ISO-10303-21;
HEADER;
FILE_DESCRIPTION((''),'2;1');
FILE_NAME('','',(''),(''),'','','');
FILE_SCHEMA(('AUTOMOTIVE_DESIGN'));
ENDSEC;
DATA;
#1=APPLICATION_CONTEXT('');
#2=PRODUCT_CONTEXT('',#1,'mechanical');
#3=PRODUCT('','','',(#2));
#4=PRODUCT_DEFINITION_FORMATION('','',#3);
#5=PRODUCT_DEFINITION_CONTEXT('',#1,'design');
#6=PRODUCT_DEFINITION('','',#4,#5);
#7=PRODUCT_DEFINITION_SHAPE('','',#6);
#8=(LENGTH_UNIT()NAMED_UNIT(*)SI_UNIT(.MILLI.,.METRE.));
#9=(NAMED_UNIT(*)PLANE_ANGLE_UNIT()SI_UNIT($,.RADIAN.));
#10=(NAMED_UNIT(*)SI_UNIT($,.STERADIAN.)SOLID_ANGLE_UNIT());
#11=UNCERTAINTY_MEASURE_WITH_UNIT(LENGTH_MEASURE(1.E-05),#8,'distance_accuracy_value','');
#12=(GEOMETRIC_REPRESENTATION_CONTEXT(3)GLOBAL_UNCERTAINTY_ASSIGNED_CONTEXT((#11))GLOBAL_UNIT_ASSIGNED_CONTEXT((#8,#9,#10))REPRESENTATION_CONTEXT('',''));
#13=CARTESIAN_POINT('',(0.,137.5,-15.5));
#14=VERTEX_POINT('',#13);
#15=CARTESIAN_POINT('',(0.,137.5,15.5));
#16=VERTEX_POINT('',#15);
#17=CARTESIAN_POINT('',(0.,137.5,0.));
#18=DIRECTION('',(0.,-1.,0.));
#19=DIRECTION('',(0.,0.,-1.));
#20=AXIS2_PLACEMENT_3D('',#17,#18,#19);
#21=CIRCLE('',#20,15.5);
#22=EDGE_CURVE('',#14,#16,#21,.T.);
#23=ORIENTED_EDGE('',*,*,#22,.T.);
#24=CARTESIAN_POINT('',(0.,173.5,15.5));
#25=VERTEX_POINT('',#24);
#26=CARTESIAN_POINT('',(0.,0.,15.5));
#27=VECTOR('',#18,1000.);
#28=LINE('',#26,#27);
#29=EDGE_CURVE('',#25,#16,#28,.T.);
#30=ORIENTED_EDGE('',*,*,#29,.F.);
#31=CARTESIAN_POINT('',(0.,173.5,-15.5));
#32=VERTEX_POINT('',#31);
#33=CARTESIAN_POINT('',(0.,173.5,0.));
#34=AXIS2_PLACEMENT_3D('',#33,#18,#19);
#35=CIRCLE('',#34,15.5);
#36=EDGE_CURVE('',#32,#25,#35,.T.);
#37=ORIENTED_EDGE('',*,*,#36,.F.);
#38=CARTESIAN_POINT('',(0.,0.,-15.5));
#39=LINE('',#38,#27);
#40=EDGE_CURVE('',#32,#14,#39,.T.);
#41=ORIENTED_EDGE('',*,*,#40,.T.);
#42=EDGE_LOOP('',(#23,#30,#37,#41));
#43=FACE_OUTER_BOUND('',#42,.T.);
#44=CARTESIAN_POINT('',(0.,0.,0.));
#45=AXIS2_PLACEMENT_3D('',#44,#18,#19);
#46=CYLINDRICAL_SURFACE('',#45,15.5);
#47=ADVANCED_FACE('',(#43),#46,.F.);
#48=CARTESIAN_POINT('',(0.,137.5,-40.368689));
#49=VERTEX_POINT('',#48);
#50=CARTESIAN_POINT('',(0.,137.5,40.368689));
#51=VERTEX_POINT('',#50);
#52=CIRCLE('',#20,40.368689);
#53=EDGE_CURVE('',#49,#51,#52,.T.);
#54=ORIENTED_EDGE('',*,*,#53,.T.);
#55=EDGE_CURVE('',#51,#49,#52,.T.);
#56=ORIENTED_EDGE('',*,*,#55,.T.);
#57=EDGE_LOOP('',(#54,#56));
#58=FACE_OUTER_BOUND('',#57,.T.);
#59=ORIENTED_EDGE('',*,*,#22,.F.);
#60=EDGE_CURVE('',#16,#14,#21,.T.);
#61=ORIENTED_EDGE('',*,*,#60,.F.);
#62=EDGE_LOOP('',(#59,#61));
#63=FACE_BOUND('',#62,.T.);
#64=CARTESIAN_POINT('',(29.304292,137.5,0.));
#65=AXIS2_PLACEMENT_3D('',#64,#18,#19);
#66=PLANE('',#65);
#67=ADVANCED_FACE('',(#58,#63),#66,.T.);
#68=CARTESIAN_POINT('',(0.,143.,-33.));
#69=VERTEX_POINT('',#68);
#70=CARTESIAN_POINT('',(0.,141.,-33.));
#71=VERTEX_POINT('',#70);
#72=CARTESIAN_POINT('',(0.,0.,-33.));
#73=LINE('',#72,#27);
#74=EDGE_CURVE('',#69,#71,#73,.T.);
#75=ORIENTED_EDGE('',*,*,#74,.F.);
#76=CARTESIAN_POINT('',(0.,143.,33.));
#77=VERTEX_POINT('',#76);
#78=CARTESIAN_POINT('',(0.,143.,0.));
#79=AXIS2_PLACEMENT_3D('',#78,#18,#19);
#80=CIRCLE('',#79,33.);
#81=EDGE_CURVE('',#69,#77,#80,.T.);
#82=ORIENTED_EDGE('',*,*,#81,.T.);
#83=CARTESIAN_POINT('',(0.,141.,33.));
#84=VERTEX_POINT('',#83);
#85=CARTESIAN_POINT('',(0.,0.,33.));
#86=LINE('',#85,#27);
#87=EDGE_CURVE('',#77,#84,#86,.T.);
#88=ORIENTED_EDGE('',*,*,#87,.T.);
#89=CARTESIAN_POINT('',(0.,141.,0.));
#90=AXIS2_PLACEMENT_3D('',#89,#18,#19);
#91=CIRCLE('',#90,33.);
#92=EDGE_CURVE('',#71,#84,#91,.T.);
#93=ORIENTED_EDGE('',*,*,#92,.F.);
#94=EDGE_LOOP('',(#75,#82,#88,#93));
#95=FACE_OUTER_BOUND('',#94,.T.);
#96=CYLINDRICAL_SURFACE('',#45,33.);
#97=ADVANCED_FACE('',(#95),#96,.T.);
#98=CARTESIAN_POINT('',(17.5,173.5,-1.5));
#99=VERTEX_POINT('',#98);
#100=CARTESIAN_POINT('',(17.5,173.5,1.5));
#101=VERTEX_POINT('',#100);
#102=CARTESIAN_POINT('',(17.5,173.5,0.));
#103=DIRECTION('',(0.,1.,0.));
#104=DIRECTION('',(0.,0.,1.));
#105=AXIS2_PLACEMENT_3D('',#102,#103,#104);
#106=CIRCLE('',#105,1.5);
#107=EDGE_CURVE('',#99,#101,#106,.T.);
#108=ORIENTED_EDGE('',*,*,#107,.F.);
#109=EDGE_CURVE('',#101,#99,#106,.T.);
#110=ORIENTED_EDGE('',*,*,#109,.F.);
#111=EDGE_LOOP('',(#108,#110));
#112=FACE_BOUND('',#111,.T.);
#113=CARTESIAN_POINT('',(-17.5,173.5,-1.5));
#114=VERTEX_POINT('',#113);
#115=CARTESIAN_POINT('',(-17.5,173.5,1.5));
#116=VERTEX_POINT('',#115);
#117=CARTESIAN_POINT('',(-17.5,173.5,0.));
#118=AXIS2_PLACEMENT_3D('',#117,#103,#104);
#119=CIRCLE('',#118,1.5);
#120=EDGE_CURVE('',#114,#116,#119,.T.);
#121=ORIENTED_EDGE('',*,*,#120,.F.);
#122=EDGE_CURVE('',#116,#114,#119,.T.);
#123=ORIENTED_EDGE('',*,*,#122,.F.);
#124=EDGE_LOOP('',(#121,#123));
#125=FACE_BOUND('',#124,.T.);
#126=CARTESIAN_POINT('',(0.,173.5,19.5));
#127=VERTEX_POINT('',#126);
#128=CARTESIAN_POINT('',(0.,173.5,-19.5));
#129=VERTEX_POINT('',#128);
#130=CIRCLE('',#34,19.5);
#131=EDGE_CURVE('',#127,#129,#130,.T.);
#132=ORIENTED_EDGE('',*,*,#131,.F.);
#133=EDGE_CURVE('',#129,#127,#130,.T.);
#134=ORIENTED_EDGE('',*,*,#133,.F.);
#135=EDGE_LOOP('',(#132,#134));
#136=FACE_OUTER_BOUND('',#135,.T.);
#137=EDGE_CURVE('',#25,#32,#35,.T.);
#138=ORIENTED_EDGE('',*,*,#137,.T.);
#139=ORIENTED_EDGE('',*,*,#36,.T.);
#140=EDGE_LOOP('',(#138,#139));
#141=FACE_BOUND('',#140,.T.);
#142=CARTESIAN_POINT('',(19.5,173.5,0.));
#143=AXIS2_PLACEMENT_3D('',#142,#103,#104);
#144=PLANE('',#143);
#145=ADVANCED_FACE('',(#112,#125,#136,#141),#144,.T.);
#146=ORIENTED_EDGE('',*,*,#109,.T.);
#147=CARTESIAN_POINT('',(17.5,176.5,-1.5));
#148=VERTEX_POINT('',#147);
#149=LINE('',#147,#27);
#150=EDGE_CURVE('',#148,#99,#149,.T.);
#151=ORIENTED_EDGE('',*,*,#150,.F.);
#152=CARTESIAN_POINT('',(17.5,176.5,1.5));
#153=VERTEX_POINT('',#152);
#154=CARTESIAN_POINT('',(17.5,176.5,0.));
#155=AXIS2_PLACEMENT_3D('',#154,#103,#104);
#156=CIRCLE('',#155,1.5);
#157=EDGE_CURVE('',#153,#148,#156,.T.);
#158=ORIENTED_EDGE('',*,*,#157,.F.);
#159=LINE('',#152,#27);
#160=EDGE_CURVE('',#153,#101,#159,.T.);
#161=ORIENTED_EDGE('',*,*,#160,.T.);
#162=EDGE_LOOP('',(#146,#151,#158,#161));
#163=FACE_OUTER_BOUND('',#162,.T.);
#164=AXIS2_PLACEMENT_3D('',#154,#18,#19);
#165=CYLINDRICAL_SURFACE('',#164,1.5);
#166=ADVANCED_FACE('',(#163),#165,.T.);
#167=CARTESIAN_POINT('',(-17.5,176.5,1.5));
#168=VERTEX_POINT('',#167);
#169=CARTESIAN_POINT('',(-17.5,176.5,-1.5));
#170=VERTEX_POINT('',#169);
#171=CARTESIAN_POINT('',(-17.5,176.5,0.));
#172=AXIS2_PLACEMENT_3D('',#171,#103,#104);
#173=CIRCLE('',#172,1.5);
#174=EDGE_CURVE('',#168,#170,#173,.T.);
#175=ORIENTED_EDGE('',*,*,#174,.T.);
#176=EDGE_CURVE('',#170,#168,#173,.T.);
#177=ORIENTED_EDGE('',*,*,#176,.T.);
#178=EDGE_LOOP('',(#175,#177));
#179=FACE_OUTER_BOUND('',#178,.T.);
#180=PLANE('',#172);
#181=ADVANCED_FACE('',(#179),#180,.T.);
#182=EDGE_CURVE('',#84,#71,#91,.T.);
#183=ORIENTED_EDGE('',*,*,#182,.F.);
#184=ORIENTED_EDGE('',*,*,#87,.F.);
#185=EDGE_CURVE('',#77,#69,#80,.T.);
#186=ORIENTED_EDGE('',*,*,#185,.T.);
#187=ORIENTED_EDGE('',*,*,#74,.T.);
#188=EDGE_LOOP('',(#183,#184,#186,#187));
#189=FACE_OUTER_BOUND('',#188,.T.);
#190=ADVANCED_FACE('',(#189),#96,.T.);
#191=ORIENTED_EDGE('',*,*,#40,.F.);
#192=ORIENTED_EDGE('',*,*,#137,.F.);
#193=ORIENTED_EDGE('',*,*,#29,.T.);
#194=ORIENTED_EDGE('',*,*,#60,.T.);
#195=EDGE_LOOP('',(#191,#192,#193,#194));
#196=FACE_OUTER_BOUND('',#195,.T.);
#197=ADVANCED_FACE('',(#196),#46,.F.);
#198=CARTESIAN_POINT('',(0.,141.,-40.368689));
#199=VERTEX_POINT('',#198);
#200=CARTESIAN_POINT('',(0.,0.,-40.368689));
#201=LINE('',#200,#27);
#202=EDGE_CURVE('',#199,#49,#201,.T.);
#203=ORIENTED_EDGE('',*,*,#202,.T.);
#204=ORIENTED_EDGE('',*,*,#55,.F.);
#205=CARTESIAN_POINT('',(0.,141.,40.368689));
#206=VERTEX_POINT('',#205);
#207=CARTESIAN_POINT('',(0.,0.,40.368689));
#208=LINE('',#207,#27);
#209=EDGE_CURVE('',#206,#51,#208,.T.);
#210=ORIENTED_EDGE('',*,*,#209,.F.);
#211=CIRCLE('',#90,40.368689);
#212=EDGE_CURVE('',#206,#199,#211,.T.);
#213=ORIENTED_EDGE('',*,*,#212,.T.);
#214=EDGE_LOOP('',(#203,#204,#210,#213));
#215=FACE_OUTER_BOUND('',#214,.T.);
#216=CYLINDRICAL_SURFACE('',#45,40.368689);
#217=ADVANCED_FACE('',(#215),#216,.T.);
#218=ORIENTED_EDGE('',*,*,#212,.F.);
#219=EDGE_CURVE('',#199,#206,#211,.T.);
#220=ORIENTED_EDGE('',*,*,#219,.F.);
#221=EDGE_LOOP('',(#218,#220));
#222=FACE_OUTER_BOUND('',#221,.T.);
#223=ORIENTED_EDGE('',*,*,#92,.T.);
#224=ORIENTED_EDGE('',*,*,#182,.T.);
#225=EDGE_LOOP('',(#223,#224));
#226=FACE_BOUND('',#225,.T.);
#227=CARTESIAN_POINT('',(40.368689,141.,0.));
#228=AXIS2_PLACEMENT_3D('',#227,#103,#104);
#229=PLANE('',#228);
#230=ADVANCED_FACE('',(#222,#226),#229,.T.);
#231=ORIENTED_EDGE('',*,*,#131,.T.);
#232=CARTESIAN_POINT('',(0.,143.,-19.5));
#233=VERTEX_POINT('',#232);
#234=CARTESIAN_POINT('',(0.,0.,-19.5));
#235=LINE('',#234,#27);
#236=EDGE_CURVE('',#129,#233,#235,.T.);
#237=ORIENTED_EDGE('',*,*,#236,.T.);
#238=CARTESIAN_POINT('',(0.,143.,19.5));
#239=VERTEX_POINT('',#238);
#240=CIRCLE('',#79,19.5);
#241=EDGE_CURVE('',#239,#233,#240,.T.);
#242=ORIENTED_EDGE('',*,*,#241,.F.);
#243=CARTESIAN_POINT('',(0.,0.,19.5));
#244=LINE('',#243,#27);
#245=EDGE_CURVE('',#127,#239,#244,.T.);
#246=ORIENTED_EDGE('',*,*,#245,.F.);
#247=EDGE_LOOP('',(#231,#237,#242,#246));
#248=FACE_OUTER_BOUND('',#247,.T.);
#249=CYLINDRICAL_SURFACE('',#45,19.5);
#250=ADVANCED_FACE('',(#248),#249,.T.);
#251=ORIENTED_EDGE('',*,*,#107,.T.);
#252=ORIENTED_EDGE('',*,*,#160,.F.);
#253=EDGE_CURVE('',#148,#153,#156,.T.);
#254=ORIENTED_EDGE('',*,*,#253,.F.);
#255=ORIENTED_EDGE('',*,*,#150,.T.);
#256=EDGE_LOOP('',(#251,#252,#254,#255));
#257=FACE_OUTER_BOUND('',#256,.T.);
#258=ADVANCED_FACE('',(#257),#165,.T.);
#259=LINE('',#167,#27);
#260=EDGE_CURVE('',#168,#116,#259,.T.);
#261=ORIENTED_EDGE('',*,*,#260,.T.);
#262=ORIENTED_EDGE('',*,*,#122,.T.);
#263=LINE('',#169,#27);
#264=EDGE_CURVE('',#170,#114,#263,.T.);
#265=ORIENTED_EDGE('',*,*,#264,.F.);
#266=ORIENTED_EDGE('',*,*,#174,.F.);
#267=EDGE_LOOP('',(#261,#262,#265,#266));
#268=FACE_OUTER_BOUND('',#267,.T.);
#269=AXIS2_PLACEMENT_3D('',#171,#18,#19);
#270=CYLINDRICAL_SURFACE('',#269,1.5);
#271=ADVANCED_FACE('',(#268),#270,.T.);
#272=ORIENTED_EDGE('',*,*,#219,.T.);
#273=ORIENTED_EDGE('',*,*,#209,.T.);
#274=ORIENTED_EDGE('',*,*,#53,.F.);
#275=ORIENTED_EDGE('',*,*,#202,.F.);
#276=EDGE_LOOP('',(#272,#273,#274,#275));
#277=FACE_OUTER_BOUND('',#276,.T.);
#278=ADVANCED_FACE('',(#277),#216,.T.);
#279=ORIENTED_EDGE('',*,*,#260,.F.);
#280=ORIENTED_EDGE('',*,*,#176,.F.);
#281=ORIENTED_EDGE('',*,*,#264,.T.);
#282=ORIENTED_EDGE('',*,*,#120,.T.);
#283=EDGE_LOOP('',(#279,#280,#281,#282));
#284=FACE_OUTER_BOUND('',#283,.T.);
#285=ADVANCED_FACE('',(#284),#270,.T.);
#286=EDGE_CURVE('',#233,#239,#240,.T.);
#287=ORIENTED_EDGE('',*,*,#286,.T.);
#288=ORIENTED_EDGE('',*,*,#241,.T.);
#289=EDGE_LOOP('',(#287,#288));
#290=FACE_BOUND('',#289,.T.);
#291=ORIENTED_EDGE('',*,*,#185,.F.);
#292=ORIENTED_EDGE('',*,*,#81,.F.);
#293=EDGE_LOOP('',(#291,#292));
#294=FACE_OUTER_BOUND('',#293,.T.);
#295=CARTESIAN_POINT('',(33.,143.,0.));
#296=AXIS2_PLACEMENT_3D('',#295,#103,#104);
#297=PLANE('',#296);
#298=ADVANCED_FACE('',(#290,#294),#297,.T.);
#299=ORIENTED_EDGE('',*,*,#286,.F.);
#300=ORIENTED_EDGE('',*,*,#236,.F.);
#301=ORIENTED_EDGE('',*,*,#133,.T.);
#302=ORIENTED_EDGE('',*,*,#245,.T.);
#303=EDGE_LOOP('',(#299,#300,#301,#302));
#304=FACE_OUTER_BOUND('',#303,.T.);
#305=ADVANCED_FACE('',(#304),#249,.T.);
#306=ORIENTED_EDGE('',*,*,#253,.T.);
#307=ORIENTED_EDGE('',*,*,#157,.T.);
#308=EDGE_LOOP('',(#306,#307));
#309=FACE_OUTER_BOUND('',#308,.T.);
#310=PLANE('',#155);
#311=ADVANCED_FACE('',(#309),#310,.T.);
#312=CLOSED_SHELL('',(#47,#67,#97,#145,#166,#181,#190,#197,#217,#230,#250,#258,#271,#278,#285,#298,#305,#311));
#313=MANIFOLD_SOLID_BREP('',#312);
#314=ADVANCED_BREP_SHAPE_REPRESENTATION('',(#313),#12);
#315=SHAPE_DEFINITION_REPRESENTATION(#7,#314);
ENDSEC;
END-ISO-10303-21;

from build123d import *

# Parameters (mm, degrees)
SKETCH2_R           = 1.5
BOSS_EXTRUDE1_DEPTH = 3


with BuildPart() as part:
    # Sketch1 → Revolve1 (revolve)
    with BuildSketch(Plane.XY, mode=Mode.PRIVATE) as revolve1_sk:
        Polygon((40.368689296, 141), (33, 141), (33, 143), (19.5, 143), (19.5, 173.5), (15.5, 173.5), (15.5, 137.5), (29.304292175, 137.5), (40.368689296, 137.5), align=None)
    revolve(revolve1_sk.sketch.rotate(Axis((0, 0, 0), (0, 1, 0)), 90), axis=Axis((0, 0, 0), (0, 1, 0)))

    # Sketch2 → Boss-Extrude1 (add)
    with BuildSketch(Plane(origin=(0, 173.5, 0), x_dir=(1, 0, 0), z_dir=(0, 1, 0))):
        with Locations(Location((17.5, 0, 0), (0, 0, 270))):
            Circle(SKETCH2_R)
        with Locations(Location((-17.5, 0, 0), (0, 0, 270))):
            Circle(SKETCH2_R)
    extrude(amount=BOSS_EXTRUDE1_DEPTH)


solid = part.part
